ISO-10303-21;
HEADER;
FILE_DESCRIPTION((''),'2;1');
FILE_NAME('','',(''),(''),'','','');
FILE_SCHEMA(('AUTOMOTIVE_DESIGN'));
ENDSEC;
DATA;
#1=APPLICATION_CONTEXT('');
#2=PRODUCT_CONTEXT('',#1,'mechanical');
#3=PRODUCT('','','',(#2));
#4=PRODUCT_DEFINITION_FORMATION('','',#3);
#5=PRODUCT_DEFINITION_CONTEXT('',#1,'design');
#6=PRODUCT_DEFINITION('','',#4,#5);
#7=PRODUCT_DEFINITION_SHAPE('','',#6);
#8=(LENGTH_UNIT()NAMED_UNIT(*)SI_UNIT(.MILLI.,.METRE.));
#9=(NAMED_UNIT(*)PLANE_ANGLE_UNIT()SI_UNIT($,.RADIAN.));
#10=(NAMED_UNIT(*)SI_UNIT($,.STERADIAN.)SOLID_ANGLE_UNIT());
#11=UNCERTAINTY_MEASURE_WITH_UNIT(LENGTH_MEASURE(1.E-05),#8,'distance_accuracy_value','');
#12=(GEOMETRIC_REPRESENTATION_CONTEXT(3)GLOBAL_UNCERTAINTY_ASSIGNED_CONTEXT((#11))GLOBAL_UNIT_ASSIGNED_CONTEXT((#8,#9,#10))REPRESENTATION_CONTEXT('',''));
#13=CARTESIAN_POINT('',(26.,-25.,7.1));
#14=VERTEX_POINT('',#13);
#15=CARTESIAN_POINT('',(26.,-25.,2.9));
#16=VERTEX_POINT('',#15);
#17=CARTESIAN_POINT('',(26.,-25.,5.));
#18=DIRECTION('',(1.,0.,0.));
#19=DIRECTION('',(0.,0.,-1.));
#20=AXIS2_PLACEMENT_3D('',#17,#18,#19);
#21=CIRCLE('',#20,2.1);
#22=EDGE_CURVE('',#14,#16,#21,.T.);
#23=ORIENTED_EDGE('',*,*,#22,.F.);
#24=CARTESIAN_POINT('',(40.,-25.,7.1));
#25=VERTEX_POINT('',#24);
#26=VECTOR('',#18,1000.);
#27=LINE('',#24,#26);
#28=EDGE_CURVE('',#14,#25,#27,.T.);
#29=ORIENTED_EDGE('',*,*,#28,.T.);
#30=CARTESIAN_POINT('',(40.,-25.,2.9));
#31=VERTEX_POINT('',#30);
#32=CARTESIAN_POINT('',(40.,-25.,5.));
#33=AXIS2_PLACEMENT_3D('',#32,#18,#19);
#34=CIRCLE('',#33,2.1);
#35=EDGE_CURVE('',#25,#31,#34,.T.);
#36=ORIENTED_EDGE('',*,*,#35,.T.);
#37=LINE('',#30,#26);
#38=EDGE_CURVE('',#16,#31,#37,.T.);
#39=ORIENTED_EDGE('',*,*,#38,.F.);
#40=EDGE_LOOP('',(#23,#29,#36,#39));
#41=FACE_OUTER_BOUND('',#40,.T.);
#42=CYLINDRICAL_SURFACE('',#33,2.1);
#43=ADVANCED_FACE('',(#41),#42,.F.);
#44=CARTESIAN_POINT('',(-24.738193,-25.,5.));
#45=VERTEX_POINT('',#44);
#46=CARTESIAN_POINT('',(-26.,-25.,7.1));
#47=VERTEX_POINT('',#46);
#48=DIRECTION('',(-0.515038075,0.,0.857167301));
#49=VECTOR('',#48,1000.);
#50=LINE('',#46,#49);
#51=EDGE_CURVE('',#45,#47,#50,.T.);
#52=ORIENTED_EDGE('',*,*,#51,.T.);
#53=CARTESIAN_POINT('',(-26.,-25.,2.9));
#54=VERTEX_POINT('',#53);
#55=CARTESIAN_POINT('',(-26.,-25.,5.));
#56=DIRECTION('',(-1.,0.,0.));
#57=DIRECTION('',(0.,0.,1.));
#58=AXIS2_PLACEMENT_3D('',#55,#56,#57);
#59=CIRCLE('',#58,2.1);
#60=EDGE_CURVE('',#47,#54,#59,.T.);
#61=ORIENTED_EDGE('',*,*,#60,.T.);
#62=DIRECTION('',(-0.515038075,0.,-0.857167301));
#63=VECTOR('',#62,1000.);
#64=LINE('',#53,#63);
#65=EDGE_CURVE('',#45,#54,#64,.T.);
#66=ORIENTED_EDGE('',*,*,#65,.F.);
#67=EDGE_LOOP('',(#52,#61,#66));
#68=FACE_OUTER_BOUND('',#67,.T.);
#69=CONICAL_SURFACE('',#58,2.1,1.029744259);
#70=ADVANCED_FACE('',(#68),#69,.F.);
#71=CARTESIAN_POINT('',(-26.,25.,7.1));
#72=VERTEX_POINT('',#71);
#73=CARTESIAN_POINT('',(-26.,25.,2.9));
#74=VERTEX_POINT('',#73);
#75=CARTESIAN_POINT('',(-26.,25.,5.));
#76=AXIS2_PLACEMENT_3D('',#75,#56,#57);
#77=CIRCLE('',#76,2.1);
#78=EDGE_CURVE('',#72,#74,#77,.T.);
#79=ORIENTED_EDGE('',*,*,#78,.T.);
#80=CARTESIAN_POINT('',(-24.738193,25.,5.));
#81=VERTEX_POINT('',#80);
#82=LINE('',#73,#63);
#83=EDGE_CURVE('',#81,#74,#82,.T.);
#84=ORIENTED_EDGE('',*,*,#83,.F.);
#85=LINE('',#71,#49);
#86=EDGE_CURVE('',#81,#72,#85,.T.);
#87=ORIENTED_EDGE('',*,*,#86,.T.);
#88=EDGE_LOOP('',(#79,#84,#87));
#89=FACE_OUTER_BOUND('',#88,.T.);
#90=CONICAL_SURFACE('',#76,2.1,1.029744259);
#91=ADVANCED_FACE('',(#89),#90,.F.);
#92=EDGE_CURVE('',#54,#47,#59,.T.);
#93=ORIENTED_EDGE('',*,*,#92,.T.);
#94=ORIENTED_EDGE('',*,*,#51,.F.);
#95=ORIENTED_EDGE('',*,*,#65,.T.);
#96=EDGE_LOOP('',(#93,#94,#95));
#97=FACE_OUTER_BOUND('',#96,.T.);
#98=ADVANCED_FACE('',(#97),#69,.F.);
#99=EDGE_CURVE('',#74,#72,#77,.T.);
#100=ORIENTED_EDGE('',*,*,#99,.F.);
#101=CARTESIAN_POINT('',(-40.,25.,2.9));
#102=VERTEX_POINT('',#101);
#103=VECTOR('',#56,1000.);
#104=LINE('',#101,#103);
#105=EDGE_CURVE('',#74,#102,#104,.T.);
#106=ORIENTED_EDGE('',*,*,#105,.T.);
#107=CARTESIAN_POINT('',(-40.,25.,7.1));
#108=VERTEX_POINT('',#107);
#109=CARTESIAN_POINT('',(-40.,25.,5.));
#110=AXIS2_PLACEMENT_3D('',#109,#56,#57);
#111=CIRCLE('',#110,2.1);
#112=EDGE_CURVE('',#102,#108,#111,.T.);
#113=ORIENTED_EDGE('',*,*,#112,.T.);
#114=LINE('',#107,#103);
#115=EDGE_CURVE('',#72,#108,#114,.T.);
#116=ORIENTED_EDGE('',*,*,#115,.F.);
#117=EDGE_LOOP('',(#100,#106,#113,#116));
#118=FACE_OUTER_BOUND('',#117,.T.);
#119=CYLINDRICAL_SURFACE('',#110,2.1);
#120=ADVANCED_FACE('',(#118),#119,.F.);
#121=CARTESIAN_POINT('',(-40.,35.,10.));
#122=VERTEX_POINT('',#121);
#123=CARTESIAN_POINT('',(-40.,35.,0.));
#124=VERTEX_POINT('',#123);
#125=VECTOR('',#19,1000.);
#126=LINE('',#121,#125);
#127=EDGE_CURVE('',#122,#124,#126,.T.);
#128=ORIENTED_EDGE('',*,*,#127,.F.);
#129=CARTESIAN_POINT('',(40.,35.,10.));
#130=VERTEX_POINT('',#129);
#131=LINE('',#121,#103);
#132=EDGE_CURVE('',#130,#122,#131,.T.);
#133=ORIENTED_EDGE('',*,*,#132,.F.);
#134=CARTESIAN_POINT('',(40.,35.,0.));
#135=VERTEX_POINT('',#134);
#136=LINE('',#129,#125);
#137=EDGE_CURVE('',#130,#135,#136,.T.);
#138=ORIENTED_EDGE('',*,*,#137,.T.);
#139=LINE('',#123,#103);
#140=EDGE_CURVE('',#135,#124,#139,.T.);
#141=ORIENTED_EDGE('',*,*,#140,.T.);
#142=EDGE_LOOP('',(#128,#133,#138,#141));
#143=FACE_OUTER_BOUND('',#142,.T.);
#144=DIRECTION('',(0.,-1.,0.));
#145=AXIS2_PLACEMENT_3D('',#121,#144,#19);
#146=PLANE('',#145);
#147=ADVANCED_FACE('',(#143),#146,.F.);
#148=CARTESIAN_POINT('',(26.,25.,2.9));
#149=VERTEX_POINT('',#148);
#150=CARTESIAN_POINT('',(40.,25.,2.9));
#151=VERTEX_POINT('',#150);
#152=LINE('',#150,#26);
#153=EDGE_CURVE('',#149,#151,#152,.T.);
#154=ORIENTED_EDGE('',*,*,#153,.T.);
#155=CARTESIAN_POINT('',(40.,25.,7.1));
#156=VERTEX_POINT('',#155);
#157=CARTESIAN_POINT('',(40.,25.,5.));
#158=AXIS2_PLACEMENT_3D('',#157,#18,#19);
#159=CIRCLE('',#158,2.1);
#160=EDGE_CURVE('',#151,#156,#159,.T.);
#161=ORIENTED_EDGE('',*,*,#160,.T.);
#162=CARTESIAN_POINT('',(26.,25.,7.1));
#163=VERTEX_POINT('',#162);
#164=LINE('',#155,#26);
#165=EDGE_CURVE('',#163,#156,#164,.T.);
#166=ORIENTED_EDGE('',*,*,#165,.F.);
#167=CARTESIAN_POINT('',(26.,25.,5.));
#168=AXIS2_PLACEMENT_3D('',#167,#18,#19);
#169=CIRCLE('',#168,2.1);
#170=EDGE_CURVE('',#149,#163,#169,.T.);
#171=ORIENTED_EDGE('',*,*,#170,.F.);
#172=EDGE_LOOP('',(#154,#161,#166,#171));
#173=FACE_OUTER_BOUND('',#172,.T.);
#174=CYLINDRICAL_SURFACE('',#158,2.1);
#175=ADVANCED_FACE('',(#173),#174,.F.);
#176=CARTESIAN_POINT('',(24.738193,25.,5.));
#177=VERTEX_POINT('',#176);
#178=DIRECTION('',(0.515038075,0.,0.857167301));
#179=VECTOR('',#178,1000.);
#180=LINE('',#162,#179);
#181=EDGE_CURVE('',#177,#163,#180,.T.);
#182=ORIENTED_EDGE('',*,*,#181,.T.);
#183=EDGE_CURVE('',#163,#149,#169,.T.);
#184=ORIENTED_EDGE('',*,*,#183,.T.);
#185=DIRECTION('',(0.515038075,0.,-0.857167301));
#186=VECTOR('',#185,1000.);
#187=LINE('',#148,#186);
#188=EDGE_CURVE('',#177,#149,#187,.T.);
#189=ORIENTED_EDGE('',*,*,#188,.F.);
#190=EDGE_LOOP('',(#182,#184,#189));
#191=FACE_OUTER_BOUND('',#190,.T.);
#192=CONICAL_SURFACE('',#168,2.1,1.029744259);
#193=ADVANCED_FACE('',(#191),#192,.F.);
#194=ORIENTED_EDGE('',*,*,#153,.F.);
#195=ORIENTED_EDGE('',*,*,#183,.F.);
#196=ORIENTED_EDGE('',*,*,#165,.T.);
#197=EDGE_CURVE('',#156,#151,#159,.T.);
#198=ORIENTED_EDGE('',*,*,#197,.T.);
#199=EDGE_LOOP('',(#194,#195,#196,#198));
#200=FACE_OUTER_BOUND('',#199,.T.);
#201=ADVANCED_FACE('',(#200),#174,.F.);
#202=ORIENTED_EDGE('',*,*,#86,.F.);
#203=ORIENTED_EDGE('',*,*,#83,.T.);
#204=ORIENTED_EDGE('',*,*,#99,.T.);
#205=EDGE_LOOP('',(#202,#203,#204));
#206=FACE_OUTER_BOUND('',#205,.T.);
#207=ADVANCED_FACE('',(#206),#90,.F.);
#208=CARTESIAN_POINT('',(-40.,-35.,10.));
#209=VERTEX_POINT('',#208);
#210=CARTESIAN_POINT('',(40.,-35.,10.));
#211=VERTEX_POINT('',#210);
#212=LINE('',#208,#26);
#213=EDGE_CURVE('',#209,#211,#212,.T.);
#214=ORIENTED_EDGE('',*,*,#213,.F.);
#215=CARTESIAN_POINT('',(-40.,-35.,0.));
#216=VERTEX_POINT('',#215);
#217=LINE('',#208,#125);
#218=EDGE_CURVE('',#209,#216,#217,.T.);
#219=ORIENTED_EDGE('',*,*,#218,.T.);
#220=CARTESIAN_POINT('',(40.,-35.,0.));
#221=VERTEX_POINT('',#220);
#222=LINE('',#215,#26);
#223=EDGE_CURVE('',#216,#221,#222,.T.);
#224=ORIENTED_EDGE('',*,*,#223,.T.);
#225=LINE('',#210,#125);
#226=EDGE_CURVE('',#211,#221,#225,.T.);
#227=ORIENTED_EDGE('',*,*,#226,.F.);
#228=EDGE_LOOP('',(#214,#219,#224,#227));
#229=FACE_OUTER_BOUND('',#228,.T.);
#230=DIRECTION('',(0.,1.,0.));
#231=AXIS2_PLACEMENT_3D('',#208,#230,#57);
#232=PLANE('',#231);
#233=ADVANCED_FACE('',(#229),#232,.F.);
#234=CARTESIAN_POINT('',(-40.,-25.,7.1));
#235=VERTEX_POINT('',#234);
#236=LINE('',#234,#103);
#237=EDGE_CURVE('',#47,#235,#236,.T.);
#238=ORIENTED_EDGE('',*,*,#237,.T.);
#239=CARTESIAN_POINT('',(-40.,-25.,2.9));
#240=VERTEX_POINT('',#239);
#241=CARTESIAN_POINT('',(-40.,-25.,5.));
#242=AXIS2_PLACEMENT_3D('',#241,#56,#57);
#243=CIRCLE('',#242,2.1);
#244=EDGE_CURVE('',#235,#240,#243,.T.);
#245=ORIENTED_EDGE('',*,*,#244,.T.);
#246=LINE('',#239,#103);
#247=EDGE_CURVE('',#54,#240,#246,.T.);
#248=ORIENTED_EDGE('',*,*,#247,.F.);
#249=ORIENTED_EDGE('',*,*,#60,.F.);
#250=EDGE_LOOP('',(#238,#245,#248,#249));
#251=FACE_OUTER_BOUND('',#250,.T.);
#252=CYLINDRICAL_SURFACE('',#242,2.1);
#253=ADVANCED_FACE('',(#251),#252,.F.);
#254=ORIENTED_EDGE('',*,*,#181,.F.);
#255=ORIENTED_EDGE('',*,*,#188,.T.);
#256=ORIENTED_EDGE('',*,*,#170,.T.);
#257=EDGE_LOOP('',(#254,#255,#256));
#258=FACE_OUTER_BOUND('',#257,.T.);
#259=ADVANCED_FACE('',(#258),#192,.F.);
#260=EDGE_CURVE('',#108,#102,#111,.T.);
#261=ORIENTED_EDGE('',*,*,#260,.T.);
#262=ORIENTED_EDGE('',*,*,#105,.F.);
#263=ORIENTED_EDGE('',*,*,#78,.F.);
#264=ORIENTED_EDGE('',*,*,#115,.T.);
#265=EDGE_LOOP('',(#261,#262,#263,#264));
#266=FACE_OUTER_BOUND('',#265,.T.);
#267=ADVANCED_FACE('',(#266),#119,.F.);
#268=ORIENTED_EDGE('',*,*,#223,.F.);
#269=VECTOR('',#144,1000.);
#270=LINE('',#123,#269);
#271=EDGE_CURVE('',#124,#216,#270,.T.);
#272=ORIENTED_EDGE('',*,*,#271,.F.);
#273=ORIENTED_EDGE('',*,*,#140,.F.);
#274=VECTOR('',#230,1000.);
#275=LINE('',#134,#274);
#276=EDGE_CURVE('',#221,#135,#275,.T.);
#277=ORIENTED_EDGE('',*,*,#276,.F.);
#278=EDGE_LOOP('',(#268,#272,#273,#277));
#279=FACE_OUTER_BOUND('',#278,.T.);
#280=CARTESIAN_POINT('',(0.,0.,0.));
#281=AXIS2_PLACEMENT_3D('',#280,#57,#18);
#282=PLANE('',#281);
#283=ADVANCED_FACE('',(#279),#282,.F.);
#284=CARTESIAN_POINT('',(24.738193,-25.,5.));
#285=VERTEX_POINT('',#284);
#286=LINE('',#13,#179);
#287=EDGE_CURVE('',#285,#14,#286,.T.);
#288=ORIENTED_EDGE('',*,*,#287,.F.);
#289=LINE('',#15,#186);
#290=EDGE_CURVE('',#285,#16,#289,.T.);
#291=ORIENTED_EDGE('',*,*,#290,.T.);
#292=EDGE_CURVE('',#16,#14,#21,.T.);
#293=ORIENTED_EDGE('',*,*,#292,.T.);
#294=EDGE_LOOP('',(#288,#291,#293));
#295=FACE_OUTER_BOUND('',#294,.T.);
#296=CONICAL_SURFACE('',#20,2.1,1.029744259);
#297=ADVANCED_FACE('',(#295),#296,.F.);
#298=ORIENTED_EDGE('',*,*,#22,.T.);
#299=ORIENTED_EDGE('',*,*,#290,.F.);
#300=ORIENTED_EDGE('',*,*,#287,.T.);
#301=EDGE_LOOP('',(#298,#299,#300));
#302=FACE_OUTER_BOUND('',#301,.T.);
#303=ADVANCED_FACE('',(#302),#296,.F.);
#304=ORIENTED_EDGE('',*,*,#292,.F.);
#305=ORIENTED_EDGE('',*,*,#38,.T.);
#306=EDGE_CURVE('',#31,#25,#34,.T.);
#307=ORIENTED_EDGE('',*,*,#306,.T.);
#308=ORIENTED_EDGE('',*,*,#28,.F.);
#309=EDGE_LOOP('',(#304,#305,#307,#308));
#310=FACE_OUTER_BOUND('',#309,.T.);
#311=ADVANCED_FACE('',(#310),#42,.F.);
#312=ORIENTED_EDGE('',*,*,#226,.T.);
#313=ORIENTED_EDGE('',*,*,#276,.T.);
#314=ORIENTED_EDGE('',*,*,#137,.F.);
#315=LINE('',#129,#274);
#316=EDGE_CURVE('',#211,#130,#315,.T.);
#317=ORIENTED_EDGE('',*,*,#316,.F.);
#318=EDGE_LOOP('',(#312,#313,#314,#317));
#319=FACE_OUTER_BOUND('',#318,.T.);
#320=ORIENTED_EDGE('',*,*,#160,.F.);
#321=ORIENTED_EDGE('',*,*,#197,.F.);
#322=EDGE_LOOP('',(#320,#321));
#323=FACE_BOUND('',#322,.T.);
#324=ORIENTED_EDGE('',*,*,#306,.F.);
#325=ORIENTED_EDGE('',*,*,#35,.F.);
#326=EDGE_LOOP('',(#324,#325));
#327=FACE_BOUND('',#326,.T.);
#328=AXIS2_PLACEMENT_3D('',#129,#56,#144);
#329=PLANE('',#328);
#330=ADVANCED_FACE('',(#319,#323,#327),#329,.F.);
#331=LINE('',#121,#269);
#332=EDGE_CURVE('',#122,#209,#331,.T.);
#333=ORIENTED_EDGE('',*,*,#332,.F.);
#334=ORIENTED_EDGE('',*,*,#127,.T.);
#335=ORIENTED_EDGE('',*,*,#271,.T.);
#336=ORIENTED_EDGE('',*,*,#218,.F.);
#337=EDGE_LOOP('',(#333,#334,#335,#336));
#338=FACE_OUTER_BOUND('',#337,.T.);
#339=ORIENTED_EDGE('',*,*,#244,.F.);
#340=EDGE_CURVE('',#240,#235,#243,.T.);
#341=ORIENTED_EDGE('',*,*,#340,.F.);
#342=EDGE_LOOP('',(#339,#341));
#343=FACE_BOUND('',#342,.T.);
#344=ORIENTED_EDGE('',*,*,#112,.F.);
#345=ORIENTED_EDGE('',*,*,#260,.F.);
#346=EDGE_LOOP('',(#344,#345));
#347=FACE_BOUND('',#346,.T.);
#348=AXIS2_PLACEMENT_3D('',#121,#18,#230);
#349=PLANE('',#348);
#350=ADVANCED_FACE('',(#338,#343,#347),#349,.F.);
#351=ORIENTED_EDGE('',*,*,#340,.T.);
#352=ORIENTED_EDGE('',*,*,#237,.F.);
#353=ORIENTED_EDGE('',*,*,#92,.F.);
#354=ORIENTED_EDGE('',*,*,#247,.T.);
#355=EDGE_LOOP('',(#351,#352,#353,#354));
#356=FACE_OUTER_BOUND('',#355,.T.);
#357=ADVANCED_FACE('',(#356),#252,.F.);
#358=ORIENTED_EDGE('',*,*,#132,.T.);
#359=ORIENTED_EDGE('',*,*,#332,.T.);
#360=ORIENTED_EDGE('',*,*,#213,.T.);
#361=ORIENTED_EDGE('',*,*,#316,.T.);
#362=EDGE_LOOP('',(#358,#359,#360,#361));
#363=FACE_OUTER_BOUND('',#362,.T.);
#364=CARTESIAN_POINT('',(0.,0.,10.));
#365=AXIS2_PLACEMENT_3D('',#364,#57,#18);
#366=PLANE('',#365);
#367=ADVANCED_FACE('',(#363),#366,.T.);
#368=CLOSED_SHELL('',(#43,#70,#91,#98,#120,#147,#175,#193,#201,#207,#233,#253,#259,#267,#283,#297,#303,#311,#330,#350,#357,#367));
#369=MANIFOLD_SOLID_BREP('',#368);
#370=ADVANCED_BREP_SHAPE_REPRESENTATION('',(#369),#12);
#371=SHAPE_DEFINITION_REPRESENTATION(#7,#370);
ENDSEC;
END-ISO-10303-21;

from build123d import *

# Parameters (mm, degrees)
SKETCH_1_W             = 80
SKETCH_1_H             = 70
EXTRUDE_1_DEPTH        = 10
HOLE_WIZARD_M5_1_D     = 4.2
HOLE_WIZARD_M5_1_DEPTH = 14
HOLE_WIZARD_M5_1_TIP   = 1.2618073
HOLE_WIZARD_M5_2_D     = 4.2
HOLE_WIZARD_M5_2_DEPTH = 14
HOLE_WIZARD_M5_2_TIP   = 1.2618073


with BuildPart() as part:
    # 草图1 → 凸台-拉伸1 (new body)
    with BuildSketch(Plane.XY):
        Rectangle(SKETCH_1_W, SKETCH_1_H)
    extrude(amount=EXTRUDE_1_DEPTH)

    # M5 螺纹孔1
    with Locations(Plane(origin=(40, 0, 0), x_dir=(0, 0, -1), z_dir=(1, 0, 0))):
        with Locations((-5, -25), (-5, 25)):
            Hole(HOLE_WIZARD_M5_1_D / 2, depth=HOLE_WIZARD_M5_1_DEPTH)
            with Locations((0, 0, -(HOLE_WIZARD_M5_1_DEPTH + HOLE_WIZARD_M5_1_TIP / 2))):  # 118° drill point
                Cone(0, HOLE_WIZARD_M5_1_D / 2, HOLE_WIZARD_M5_1_TIP, mode=Mode.SUBTRACT)

    # M5 螺纹孔2
    with Locations(Plane.ZY.offset(40)):
        with Locations((5, 25), (5, -25)):
            Hole(HOLE_WIZARD_M5_2_D / 2, depth=HOLE_WIZARD_M5_2_DEPTH)
            with Locations((0, 0, -(HOLE_WIZARD_M5_2_DEPTH + HOLE_WIZARD_M5_2_TIP / 2))):  # 118° drill point
                Cone(0, HOLE_WIZARD_M5_2_D / 2, HOLE_WIZARD_M5_2_TIP, mode=Mode.SUBTRACT)


solid = part.part
